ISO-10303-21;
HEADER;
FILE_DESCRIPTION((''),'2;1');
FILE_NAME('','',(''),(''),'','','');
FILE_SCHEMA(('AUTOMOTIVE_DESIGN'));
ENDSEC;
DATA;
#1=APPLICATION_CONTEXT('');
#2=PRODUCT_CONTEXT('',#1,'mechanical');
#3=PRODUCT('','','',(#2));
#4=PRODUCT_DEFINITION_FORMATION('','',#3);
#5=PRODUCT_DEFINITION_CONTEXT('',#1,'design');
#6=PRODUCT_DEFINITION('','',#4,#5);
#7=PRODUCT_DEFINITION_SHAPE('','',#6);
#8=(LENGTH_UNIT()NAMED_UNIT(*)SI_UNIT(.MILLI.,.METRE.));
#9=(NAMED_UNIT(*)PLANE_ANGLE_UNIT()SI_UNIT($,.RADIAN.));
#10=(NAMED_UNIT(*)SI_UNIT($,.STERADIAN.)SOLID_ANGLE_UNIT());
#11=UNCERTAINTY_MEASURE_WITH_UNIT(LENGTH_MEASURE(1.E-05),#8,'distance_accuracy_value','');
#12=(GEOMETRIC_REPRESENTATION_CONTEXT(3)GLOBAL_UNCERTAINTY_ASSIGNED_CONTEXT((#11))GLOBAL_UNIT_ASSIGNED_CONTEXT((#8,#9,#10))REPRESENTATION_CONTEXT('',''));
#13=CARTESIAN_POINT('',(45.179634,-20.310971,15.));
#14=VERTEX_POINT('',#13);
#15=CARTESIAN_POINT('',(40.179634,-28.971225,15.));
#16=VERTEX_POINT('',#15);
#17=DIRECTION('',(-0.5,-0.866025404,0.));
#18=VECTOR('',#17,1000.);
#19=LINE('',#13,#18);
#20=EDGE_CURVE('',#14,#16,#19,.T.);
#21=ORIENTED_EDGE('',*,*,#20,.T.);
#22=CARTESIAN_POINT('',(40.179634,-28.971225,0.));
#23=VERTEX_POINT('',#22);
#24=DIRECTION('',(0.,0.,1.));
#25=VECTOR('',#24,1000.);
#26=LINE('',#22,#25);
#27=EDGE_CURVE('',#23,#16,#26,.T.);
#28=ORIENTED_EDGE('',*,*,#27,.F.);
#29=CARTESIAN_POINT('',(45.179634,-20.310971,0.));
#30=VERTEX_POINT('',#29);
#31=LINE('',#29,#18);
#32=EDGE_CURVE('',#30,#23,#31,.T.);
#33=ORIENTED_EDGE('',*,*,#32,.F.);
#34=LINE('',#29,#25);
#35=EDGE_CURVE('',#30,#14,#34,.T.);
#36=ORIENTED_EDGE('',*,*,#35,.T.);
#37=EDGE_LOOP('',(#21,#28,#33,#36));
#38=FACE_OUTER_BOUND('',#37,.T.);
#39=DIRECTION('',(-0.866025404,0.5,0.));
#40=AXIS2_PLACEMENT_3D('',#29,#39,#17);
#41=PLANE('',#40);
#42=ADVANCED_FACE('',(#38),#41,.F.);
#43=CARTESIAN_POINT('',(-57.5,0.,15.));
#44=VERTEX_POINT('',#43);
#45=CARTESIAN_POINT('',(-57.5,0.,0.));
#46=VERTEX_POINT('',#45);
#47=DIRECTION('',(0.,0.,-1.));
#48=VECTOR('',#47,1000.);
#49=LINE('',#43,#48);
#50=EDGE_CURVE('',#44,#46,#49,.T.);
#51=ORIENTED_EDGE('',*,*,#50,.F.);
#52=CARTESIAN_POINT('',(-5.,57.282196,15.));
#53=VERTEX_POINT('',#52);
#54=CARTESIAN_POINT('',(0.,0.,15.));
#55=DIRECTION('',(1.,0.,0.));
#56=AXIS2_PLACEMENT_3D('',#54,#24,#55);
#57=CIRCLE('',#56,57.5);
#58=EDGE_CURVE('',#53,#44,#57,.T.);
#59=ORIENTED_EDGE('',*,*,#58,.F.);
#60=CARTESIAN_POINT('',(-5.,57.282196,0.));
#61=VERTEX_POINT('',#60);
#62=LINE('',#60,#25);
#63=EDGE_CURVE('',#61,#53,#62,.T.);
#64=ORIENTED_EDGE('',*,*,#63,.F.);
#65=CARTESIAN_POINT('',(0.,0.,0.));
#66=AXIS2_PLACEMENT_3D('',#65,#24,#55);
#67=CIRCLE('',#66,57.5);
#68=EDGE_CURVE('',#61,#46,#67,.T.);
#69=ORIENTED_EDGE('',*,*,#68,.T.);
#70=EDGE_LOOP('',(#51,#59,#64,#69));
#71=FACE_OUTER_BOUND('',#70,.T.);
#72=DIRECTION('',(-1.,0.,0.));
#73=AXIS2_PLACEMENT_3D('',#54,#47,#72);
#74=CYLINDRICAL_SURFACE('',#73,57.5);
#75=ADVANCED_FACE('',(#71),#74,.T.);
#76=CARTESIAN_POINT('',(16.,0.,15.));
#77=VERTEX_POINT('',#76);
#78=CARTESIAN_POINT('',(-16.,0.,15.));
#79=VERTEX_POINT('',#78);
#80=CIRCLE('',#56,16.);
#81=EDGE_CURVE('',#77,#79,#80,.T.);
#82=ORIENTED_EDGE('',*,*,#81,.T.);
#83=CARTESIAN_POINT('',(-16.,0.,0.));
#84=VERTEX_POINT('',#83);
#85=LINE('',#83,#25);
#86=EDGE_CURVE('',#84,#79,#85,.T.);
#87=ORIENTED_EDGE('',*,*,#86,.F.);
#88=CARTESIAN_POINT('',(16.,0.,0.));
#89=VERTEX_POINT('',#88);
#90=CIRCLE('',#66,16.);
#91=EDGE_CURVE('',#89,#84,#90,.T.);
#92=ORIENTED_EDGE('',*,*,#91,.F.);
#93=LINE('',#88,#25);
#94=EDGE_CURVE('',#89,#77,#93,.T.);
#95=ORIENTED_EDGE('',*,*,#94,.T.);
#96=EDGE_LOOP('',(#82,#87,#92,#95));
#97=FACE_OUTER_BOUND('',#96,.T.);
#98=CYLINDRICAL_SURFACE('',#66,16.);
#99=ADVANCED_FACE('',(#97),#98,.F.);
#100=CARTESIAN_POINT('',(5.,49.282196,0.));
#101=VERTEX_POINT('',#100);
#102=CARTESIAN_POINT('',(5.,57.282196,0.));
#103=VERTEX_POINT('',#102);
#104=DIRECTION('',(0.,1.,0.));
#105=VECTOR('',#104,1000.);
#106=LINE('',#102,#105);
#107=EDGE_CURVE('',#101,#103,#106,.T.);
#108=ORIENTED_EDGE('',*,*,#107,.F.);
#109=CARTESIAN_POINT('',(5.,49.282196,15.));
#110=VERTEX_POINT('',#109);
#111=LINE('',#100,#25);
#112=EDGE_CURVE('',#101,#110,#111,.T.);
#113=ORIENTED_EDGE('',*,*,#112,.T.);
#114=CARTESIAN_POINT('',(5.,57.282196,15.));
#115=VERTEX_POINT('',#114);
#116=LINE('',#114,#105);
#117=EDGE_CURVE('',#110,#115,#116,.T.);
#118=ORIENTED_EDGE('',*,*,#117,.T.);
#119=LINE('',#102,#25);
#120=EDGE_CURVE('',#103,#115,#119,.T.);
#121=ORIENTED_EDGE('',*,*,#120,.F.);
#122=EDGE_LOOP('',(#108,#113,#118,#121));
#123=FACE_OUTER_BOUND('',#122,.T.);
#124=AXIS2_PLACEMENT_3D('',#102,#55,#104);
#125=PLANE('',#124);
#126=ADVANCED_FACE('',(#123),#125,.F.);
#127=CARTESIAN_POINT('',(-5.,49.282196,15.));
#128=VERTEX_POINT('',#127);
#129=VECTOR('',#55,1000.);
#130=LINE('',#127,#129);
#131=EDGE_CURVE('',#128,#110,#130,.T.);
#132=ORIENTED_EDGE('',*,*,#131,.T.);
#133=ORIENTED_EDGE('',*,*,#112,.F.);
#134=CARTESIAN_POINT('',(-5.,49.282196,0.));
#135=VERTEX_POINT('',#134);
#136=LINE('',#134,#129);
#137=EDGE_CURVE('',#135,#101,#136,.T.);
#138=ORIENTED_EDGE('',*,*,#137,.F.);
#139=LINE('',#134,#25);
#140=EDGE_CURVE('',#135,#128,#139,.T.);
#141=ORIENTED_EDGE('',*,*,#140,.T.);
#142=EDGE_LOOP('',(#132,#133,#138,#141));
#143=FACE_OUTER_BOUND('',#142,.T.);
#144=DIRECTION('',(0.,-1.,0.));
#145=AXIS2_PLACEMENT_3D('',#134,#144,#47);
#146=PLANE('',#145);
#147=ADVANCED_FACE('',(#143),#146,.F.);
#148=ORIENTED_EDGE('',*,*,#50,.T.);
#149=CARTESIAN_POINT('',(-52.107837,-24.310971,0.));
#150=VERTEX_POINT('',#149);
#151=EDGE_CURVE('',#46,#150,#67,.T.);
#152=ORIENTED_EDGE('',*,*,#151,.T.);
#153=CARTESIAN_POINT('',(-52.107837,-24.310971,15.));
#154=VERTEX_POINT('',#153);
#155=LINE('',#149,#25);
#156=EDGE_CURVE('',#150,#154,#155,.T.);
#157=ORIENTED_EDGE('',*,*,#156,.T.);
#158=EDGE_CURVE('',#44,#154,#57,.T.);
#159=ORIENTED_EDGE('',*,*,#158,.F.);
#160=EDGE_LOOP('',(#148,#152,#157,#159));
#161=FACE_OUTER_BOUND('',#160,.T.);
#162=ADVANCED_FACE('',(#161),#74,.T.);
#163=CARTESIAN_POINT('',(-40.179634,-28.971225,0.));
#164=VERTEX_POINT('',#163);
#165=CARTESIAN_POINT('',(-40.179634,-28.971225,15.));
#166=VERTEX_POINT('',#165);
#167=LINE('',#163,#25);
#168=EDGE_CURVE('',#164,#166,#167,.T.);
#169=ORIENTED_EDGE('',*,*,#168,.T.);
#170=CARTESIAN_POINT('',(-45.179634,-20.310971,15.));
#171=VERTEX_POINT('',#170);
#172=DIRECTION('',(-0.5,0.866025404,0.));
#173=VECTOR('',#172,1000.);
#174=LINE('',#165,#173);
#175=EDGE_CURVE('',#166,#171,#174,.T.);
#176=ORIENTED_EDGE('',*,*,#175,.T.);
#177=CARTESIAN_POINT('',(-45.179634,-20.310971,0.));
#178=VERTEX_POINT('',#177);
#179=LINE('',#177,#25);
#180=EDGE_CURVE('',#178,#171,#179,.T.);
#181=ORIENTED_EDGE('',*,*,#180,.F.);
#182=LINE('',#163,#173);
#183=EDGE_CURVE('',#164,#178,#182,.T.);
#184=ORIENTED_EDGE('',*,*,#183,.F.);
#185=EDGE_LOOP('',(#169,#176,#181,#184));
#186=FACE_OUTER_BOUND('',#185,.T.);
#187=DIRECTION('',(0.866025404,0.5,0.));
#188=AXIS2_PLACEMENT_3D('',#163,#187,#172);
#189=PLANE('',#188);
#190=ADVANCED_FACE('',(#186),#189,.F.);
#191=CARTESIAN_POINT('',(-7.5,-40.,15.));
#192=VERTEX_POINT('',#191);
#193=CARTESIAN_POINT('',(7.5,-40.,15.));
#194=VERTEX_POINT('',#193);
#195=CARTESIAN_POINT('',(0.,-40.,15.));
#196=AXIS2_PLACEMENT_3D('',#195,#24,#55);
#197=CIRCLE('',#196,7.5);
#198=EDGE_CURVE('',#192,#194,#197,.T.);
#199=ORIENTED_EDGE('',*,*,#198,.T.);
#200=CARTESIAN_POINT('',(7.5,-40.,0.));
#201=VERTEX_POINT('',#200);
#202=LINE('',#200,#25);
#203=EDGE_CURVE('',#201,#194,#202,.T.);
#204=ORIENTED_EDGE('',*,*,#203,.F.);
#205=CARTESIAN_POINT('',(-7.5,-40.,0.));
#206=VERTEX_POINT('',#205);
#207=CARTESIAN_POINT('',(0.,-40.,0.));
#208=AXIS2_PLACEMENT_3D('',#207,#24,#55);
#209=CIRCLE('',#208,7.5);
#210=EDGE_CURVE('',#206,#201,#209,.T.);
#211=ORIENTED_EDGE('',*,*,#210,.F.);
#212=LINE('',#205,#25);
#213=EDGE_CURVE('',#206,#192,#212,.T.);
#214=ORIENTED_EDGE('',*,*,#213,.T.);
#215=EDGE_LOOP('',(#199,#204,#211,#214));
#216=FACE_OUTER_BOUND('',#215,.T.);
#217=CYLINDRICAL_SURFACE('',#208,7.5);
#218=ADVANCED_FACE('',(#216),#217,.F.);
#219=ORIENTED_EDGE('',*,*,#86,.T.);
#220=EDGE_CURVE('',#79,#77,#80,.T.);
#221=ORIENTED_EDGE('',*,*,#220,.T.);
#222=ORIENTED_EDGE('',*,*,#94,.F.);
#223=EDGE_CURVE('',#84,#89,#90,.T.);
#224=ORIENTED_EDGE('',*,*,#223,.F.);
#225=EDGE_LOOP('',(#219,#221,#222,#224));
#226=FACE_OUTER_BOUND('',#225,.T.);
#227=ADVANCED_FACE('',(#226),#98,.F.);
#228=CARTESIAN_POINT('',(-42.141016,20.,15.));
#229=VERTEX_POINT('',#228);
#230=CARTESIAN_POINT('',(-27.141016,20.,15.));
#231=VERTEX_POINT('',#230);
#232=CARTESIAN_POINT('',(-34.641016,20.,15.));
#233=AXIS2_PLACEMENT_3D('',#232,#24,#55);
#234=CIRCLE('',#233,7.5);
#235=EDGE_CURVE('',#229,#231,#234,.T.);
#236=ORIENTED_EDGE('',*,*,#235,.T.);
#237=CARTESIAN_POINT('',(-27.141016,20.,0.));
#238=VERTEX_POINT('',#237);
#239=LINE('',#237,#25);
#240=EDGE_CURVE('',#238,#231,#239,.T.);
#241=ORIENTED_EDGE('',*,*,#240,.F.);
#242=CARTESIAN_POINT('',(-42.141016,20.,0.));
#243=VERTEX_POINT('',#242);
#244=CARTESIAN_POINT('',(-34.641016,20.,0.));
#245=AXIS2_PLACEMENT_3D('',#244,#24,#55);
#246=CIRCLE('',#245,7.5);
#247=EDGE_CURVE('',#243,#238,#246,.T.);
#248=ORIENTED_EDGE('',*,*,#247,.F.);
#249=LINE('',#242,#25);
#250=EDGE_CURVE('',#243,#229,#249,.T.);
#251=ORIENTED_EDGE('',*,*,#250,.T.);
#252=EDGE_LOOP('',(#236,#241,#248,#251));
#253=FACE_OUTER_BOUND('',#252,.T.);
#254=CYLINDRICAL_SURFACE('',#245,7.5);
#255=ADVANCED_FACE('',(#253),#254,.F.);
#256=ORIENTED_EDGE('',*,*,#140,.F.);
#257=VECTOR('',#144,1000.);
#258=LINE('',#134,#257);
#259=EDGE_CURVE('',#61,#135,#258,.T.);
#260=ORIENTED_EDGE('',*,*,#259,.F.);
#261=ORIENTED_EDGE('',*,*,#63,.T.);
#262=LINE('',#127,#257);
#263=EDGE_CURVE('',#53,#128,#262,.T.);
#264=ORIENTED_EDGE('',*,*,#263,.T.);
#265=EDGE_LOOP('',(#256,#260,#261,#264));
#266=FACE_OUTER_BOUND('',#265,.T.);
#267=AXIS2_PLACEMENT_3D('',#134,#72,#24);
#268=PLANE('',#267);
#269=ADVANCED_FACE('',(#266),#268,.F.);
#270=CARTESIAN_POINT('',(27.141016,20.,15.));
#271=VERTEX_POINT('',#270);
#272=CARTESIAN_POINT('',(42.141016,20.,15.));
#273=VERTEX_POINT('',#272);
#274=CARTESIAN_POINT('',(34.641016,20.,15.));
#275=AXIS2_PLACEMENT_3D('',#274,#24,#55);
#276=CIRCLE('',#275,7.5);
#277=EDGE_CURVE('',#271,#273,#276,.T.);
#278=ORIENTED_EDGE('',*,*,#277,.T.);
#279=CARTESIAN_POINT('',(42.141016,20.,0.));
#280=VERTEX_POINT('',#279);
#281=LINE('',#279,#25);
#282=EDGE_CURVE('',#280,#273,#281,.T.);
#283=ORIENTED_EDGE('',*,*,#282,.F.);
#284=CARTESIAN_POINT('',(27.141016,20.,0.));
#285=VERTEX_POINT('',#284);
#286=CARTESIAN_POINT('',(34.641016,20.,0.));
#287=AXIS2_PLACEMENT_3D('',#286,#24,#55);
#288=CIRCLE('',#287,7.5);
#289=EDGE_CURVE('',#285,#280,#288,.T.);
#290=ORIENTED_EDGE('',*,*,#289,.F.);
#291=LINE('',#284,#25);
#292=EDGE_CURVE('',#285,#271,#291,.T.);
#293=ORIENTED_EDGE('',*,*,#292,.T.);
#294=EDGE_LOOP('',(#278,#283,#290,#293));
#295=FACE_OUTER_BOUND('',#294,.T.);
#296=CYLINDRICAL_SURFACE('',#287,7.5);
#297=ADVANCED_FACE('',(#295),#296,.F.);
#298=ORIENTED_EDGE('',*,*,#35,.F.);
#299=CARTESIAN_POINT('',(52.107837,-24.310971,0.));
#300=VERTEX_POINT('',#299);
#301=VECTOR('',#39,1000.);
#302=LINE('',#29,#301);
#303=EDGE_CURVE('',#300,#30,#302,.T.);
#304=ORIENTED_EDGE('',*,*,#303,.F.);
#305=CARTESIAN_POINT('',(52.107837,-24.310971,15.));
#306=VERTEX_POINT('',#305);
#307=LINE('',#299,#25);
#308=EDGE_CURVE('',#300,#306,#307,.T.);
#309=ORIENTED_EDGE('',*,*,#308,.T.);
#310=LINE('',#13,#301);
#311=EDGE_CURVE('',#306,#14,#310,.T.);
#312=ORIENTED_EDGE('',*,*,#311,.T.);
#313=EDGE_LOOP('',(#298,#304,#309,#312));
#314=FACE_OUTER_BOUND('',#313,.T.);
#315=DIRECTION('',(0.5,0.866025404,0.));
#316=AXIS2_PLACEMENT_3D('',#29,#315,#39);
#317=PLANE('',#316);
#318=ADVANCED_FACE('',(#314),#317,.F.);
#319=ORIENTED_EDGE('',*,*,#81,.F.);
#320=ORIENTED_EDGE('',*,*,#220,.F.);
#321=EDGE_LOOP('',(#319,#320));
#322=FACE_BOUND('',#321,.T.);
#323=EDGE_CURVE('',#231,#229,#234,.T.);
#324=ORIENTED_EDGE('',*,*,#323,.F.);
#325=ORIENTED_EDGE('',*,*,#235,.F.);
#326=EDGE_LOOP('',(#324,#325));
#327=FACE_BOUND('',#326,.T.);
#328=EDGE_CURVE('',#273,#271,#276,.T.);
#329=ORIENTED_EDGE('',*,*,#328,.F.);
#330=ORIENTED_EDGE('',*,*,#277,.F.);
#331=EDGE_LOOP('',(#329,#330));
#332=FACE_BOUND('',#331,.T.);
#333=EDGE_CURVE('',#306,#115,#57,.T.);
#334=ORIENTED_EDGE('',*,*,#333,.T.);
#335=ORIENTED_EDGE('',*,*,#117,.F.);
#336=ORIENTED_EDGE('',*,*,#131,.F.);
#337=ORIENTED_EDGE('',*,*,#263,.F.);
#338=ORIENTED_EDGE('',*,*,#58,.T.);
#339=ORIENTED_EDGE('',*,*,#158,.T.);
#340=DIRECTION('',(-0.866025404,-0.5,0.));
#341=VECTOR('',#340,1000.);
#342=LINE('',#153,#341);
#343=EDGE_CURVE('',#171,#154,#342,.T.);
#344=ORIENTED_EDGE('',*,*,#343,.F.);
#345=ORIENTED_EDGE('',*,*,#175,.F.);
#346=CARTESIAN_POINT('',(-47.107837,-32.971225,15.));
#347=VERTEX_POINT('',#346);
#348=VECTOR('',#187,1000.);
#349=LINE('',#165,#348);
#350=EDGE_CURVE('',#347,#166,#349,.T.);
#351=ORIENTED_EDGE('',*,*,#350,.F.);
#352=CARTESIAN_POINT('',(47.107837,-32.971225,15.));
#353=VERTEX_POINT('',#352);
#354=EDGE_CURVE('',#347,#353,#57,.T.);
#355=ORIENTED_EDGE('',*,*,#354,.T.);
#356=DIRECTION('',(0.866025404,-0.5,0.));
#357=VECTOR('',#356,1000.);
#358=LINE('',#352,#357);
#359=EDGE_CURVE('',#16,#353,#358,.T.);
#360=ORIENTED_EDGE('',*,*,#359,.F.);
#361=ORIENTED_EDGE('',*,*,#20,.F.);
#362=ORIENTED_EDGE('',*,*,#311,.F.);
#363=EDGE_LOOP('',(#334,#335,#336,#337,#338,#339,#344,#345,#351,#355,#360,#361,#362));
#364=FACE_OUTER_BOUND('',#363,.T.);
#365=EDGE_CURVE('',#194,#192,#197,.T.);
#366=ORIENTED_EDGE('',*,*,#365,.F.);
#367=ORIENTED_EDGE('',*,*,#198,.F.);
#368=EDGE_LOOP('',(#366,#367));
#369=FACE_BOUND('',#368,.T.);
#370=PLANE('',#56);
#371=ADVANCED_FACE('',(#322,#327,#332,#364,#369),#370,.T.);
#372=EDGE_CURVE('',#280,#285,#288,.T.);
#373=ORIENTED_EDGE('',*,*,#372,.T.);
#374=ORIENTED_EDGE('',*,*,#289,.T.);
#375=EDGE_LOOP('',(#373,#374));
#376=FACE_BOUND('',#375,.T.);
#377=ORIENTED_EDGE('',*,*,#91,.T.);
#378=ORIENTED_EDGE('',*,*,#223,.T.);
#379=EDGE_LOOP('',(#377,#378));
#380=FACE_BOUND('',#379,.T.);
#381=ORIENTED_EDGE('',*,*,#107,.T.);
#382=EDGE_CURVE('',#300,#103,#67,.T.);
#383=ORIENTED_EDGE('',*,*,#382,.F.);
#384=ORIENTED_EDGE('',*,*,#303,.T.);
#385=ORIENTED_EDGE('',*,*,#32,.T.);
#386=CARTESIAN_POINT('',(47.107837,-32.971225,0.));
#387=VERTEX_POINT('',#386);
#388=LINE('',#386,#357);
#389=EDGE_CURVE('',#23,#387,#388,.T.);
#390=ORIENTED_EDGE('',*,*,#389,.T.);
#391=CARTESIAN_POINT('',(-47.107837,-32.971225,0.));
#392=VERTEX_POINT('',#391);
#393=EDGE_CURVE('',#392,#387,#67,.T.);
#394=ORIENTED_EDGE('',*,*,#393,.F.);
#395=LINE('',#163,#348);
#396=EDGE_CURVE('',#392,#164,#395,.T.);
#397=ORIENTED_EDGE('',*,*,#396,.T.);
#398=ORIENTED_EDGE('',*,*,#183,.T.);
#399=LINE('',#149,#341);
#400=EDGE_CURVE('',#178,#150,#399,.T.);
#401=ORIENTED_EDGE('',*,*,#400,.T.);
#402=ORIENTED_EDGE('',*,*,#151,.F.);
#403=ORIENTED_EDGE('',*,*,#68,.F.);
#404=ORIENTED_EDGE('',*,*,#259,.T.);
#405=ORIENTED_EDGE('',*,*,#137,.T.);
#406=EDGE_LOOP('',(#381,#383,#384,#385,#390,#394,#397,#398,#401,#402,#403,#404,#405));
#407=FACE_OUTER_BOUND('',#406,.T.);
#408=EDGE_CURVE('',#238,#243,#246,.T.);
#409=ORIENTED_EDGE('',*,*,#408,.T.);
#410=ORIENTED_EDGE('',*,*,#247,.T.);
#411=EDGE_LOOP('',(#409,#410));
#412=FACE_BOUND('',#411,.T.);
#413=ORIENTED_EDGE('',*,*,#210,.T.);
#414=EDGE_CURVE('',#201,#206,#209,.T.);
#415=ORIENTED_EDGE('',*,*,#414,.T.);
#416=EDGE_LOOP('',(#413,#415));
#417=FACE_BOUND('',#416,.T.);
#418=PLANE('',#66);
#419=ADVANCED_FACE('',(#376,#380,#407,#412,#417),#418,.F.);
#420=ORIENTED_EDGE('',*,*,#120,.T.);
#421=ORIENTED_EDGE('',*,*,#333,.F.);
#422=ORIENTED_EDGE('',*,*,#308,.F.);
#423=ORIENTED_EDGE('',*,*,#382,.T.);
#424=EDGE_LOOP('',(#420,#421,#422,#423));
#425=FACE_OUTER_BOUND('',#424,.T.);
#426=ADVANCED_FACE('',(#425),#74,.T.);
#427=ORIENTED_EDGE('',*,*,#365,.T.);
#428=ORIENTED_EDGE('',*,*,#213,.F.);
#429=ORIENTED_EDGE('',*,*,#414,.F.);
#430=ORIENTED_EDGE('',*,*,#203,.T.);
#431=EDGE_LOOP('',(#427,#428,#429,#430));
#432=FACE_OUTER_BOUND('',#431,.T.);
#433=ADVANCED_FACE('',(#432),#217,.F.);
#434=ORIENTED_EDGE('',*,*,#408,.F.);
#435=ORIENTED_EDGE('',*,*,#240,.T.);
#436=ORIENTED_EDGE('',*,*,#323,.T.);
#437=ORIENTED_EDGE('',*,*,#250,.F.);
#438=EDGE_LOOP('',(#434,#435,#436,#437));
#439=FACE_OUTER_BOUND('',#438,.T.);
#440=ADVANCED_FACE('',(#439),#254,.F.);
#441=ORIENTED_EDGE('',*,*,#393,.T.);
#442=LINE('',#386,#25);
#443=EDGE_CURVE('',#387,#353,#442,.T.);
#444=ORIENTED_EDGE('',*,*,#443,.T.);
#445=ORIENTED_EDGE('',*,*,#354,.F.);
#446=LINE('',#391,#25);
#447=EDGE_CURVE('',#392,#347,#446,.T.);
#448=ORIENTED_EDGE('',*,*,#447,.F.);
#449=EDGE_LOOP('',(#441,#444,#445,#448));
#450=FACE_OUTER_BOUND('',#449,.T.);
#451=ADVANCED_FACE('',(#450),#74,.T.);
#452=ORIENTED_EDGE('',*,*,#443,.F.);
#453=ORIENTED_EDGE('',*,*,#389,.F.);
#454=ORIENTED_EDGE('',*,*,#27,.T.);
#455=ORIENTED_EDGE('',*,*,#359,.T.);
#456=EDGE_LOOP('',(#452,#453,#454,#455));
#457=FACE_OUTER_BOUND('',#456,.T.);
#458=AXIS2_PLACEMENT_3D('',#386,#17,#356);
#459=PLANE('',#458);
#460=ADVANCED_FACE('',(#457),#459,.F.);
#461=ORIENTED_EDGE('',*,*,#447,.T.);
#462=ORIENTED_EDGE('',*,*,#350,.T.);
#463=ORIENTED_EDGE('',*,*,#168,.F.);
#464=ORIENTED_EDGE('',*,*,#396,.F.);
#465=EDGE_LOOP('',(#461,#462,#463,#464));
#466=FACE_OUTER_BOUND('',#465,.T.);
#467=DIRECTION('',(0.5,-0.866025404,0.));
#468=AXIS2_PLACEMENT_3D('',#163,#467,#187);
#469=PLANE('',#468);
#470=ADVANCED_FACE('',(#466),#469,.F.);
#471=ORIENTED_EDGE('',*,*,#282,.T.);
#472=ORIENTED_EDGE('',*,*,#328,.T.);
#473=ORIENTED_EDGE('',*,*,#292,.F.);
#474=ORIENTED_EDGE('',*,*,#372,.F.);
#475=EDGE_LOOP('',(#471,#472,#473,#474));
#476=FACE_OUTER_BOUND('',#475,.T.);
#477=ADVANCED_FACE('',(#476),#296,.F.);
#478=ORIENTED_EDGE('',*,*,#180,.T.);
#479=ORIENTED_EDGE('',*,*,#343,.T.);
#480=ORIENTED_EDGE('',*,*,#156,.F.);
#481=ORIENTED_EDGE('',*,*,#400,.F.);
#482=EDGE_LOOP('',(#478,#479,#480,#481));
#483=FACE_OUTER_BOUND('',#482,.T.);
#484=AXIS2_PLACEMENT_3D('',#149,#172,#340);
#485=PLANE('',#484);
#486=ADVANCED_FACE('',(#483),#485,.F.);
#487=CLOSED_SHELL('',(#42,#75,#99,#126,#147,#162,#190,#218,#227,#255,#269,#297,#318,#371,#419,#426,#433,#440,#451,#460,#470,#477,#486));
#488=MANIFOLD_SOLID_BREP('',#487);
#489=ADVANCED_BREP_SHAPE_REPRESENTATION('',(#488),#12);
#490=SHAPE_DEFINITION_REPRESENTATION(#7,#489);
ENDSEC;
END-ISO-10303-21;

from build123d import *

# Parameters (mm, degrees)
DISC_PROFILE_115_R      = 57.5
DISC_115X15_DEPTH       = 15
HOLES_4X_15_SKETCH_R    = 7.5
HOLES_4X_15_ON_80_DEPTH = 15
CENTRE_BORE_32_SKETCH_R = 16
CENTRE_BORE_32_DEPTH    = 15
RIM_START               = -15
RIM_NOTCHES_DEPTH       = 15


with BuildPart() as part:
    # Disc Profile Ø115 → Disc Ø115x15 (new body)
    with BuildSketch(Plane.XY):
        Circle(DISC_PROFILE_115_R)
    extrude(amount=DISC_115X15_DEPTH)

    # Holes 4xØ15 Sketch → Holes 4xØ15 on Ø80 (cut)
    with BuildSketch(Plane.XY.offset(15)):
        with Locations((34.641016151, 20)):
            Circle(HOLES_4X_15_SKETCH_R)
        with Locations((0, -40)):
            Circle(HOLES_4X_15_SKETCH_R)
        with Locations((-34.641016151, 20)):
            Circle(HOLES_4X_15_SKETCH_R)
    extrude(amount=-HOLES_4X_15_ON_80_DEPTH, mode=Mode.SUBTRACT)

    # Centre Bore Ø32 Sketch → Centre Bore Ø32 (cut)
    with BuildSketch(Plane.XY.offset(15)):
        Circle(CENTRE_BORE_32_SKETCH_R)
    extrude(amount=-CENTRE_BORE_32_DEPTH, mode=Mode.SUBTRACT)

    # Rim Notches Sketch → Rim Notches (cut)
    with BuildSketch(Plane.XY.offset(15).offset(RIM_START)):
        with BuildLine():
            Line((-5, 49.282196187), (5, 49.282196187))
            Line((5, 49.282196187), (5, 57.282196187))
            ThreePointArc((5, 57.282196187), (0, 57.5), (-5, 57.282196187))
            Line((-5, 57.282196187), (-5, 49.282196187))
        make_face()
        with BuildLine():
            Line((45.179633852, -20.310971075), (40.179633852, -28.971225112))
            Line((40.179633852, -28.971225112), (47.107837082, -32.971225112))
            ThreePointArc((47.107837082, -32.971225112), (49.796460718, -28.75), (52.107837082, -24.310971075))
            Line((52.107837082, -24.310971075), (45.179633852, -20.310971075))
        make_face()
        with BuildLine():
            Line((-40.179633852, -28.971225112), (-45.179633852, -20.310971075))
            Line((-45.179633852, -20.310971075), (-52.107837082, -24.310971075))
            ThreePointArc((-52.107837082, -24.310971075), (-49.796460718, -28.75), (-47.107837082, -32.971225112))
            Line((-47.107837082, -32.971225112), (-40.179633852, -28.971225112))
        make_face()
    extrude(amount=RIM_NOTCHES_DEPTH, mode=Mode.SUBTRACT)


solid = part.part
